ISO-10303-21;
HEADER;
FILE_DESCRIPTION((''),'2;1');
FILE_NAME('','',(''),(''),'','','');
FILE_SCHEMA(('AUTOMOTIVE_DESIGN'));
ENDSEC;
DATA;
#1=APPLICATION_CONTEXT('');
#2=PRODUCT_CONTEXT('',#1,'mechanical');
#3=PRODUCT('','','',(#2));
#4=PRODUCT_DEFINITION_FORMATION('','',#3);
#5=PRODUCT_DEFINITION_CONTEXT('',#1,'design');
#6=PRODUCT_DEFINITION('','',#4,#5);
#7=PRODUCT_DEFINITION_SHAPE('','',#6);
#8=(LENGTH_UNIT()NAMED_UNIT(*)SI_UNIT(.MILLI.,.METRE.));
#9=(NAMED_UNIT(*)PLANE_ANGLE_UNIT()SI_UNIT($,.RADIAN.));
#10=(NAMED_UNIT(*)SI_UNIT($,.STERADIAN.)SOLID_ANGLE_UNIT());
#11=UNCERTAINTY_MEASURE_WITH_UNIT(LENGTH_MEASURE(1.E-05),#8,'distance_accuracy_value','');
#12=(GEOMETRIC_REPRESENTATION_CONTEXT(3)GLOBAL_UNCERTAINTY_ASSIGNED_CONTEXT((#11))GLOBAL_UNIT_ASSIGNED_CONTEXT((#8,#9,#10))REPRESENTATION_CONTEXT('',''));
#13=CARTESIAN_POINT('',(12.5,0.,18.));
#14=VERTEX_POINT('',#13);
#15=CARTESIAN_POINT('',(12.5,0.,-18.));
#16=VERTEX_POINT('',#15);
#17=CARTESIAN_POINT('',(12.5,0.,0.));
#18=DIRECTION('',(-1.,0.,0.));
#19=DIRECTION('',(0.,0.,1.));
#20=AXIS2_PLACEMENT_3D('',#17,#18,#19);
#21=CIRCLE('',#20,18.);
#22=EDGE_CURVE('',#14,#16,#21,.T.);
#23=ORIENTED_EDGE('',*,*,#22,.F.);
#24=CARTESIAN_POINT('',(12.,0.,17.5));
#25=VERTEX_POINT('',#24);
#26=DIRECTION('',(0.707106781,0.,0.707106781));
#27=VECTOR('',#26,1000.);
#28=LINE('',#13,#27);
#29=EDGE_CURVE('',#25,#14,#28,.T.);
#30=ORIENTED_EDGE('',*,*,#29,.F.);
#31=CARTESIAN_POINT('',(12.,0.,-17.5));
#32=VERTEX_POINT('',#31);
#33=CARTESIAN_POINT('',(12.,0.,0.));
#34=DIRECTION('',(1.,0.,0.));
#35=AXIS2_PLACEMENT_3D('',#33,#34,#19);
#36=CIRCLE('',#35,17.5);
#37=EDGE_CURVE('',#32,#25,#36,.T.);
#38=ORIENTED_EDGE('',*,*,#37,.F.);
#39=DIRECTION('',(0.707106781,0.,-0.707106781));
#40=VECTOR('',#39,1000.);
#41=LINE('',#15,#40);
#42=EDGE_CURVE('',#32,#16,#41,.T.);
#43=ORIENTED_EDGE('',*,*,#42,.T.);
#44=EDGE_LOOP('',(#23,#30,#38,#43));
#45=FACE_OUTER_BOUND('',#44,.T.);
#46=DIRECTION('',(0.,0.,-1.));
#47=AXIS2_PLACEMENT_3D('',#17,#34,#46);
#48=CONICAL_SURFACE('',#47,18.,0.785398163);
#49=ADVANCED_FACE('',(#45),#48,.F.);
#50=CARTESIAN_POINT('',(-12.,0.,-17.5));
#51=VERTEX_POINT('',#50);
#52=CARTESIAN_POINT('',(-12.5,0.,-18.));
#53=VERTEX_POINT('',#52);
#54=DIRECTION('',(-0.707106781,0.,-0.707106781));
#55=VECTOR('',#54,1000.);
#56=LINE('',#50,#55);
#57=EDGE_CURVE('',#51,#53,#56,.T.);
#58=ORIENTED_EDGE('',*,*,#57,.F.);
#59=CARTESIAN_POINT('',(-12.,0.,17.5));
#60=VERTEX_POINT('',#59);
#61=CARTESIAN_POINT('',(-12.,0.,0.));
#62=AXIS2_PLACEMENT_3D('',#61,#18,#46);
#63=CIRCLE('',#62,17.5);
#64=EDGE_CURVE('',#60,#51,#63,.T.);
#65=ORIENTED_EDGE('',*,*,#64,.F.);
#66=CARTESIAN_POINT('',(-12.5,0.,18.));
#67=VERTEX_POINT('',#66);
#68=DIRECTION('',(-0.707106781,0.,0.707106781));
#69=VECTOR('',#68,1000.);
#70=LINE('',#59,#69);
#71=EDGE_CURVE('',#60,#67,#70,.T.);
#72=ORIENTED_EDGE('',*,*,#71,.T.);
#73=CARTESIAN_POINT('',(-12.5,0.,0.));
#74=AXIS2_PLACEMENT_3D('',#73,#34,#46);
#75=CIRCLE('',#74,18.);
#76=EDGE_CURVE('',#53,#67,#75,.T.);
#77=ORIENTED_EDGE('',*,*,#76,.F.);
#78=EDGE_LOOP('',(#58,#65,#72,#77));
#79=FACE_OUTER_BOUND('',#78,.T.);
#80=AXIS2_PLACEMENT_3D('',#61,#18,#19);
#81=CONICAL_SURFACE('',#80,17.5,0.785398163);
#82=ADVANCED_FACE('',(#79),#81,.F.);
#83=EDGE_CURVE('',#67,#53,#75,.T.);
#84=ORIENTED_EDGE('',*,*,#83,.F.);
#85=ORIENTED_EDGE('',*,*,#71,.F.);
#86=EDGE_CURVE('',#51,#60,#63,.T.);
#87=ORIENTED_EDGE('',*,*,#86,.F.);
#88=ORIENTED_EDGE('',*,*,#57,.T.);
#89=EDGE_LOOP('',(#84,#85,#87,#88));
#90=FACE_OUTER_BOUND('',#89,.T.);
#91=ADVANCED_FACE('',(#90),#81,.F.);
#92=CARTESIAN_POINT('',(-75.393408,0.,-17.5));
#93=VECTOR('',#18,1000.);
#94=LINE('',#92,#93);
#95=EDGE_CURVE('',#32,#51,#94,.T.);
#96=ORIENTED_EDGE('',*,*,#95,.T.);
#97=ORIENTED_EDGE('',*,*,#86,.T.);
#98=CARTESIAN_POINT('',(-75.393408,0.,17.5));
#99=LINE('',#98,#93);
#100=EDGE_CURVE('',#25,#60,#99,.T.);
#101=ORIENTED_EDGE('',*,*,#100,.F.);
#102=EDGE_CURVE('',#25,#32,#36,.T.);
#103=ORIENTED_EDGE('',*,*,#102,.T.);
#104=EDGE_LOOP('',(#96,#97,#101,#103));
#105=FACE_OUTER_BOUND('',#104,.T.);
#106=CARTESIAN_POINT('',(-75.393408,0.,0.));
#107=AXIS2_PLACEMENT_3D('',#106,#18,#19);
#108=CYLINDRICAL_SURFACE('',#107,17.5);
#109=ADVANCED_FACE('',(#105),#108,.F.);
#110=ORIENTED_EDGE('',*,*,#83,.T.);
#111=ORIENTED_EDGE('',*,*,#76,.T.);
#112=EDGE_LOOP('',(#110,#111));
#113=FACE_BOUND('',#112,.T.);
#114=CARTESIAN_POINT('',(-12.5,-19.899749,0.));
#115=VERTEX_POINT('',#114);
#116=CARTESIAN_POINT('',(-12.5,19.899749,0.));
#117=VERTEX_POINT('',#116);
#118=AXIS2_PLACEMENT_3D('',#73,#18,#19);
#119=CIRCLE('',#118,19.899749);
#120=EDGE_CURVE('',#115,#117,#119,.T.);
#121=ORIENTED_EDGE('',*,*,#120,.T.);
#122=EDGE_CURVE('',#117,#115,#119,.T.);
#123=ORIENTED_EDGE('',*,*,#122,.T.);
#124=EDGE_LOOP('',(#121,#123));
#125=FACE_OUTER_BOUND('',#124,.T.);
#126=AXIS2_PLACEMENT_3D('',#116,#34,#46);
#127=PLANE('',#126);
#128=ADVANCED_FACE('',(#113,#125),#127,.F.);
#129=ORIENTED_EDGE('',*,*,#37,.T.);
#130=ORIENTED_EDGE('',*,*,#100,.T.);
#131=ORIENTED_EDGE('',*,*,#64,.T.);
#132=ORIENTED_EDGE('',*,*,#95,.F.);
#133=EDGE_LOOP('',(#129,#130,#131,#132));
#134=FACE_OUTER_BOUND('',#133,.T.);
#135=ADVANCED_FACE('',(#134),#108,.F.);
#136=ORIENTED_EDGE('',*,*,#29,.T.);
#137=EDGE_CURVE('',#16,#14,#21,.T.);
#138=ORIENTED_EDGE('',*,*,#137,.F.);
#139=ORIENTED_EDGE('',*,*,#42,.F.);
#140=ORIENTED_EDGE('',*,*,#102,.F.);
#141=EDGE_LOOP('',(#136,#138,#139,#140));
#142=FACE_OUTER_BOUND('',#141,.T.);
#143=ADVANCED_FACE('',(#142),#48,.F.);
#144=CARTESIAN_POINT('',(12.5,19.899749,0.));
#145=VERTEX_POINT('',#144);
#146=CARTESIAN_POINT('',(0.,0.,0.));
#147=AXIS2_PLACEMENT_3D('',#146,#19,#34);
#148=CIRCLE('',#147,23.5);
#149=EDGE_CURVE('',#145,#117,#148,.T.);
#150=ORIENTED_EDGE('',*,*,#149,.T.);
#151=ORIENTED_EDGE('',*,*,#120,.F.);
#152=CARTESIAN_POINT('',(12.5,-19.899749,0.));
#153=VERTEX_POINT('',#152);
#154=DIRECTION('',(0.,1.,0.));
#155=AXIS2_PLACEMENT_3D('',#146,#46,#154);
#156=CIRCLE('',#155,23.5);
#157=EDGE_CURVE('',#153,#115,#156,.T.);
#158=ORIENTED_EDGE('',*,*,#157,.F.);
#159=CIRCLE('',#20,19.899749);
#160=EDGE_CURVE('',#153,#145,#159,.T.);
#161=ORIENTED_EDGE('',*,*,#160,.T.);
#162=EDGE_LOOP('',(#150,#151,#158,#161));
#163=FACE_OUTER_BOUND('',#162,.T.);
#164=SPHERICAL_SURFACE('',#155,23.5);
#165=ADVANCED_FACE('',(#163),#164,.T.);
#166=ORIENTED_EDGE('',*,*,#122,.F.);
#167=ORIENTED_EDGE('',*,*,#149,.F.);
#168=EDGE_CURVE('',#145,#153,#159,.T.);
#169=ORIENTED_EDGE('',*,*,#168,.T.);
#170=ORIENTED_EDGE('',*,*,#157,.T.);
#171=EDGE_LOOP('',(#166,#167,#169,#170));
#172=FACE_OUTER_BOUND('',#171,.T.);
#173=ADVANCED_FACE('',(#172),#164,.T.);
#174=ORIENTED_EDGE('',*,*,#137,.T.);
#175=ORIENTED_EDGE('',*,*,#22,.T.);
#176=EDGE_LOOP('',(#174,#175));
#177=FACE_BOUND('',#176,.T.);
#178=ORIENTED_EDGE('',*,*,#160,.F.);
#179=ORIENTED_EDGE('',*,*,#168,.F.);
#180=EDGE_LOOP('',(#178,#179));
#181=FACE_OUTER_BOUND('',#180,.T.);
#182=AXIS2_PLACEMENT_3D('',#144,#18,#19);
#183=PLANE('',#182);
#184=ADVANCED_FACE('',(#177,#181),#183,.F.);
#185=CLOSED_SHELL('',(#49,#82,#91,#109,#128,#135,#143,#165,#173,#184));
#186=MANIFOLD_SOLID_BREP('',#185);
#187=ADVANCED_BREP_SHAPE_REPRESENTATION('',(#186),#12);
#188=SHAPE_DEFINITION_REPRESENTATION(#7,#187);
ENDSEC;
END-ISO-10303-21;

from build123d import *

# Parameters (mm, degrees)
CHAMFER_1_SIZE = 0.5


with BuildPart() as part:
    # 草图1 → 旋转1 (revolve)
    with BuildSketch(Plane.XY):
        with BuildLine():
            Line((-12.5, 19.899748742), (-12.5, 17.5))
            Line((-12.5, 17.5), (12.5, 17.5))
            Line((12.5, 17.5), (12.5, 19.899748742))
            ThreePointArc((12.5, 19.899748742), (0, 23.5), (-12.5, 19.899748742))
        make_face()
    revolve(axis=Axis((-75.39340763, 0, 0), (1, 0, 0)))

    # 倒角1
    chamfer_1_edges = [part.edges().sort_by_distance(p)[0] for p in [
        (12.5, -17.5, 0),
        (-12.5, -17.5, 0),
    ]]
    chamfer(chamfer_1_edges, length=CHAMFER_1_SIZE)


solid = part.part
